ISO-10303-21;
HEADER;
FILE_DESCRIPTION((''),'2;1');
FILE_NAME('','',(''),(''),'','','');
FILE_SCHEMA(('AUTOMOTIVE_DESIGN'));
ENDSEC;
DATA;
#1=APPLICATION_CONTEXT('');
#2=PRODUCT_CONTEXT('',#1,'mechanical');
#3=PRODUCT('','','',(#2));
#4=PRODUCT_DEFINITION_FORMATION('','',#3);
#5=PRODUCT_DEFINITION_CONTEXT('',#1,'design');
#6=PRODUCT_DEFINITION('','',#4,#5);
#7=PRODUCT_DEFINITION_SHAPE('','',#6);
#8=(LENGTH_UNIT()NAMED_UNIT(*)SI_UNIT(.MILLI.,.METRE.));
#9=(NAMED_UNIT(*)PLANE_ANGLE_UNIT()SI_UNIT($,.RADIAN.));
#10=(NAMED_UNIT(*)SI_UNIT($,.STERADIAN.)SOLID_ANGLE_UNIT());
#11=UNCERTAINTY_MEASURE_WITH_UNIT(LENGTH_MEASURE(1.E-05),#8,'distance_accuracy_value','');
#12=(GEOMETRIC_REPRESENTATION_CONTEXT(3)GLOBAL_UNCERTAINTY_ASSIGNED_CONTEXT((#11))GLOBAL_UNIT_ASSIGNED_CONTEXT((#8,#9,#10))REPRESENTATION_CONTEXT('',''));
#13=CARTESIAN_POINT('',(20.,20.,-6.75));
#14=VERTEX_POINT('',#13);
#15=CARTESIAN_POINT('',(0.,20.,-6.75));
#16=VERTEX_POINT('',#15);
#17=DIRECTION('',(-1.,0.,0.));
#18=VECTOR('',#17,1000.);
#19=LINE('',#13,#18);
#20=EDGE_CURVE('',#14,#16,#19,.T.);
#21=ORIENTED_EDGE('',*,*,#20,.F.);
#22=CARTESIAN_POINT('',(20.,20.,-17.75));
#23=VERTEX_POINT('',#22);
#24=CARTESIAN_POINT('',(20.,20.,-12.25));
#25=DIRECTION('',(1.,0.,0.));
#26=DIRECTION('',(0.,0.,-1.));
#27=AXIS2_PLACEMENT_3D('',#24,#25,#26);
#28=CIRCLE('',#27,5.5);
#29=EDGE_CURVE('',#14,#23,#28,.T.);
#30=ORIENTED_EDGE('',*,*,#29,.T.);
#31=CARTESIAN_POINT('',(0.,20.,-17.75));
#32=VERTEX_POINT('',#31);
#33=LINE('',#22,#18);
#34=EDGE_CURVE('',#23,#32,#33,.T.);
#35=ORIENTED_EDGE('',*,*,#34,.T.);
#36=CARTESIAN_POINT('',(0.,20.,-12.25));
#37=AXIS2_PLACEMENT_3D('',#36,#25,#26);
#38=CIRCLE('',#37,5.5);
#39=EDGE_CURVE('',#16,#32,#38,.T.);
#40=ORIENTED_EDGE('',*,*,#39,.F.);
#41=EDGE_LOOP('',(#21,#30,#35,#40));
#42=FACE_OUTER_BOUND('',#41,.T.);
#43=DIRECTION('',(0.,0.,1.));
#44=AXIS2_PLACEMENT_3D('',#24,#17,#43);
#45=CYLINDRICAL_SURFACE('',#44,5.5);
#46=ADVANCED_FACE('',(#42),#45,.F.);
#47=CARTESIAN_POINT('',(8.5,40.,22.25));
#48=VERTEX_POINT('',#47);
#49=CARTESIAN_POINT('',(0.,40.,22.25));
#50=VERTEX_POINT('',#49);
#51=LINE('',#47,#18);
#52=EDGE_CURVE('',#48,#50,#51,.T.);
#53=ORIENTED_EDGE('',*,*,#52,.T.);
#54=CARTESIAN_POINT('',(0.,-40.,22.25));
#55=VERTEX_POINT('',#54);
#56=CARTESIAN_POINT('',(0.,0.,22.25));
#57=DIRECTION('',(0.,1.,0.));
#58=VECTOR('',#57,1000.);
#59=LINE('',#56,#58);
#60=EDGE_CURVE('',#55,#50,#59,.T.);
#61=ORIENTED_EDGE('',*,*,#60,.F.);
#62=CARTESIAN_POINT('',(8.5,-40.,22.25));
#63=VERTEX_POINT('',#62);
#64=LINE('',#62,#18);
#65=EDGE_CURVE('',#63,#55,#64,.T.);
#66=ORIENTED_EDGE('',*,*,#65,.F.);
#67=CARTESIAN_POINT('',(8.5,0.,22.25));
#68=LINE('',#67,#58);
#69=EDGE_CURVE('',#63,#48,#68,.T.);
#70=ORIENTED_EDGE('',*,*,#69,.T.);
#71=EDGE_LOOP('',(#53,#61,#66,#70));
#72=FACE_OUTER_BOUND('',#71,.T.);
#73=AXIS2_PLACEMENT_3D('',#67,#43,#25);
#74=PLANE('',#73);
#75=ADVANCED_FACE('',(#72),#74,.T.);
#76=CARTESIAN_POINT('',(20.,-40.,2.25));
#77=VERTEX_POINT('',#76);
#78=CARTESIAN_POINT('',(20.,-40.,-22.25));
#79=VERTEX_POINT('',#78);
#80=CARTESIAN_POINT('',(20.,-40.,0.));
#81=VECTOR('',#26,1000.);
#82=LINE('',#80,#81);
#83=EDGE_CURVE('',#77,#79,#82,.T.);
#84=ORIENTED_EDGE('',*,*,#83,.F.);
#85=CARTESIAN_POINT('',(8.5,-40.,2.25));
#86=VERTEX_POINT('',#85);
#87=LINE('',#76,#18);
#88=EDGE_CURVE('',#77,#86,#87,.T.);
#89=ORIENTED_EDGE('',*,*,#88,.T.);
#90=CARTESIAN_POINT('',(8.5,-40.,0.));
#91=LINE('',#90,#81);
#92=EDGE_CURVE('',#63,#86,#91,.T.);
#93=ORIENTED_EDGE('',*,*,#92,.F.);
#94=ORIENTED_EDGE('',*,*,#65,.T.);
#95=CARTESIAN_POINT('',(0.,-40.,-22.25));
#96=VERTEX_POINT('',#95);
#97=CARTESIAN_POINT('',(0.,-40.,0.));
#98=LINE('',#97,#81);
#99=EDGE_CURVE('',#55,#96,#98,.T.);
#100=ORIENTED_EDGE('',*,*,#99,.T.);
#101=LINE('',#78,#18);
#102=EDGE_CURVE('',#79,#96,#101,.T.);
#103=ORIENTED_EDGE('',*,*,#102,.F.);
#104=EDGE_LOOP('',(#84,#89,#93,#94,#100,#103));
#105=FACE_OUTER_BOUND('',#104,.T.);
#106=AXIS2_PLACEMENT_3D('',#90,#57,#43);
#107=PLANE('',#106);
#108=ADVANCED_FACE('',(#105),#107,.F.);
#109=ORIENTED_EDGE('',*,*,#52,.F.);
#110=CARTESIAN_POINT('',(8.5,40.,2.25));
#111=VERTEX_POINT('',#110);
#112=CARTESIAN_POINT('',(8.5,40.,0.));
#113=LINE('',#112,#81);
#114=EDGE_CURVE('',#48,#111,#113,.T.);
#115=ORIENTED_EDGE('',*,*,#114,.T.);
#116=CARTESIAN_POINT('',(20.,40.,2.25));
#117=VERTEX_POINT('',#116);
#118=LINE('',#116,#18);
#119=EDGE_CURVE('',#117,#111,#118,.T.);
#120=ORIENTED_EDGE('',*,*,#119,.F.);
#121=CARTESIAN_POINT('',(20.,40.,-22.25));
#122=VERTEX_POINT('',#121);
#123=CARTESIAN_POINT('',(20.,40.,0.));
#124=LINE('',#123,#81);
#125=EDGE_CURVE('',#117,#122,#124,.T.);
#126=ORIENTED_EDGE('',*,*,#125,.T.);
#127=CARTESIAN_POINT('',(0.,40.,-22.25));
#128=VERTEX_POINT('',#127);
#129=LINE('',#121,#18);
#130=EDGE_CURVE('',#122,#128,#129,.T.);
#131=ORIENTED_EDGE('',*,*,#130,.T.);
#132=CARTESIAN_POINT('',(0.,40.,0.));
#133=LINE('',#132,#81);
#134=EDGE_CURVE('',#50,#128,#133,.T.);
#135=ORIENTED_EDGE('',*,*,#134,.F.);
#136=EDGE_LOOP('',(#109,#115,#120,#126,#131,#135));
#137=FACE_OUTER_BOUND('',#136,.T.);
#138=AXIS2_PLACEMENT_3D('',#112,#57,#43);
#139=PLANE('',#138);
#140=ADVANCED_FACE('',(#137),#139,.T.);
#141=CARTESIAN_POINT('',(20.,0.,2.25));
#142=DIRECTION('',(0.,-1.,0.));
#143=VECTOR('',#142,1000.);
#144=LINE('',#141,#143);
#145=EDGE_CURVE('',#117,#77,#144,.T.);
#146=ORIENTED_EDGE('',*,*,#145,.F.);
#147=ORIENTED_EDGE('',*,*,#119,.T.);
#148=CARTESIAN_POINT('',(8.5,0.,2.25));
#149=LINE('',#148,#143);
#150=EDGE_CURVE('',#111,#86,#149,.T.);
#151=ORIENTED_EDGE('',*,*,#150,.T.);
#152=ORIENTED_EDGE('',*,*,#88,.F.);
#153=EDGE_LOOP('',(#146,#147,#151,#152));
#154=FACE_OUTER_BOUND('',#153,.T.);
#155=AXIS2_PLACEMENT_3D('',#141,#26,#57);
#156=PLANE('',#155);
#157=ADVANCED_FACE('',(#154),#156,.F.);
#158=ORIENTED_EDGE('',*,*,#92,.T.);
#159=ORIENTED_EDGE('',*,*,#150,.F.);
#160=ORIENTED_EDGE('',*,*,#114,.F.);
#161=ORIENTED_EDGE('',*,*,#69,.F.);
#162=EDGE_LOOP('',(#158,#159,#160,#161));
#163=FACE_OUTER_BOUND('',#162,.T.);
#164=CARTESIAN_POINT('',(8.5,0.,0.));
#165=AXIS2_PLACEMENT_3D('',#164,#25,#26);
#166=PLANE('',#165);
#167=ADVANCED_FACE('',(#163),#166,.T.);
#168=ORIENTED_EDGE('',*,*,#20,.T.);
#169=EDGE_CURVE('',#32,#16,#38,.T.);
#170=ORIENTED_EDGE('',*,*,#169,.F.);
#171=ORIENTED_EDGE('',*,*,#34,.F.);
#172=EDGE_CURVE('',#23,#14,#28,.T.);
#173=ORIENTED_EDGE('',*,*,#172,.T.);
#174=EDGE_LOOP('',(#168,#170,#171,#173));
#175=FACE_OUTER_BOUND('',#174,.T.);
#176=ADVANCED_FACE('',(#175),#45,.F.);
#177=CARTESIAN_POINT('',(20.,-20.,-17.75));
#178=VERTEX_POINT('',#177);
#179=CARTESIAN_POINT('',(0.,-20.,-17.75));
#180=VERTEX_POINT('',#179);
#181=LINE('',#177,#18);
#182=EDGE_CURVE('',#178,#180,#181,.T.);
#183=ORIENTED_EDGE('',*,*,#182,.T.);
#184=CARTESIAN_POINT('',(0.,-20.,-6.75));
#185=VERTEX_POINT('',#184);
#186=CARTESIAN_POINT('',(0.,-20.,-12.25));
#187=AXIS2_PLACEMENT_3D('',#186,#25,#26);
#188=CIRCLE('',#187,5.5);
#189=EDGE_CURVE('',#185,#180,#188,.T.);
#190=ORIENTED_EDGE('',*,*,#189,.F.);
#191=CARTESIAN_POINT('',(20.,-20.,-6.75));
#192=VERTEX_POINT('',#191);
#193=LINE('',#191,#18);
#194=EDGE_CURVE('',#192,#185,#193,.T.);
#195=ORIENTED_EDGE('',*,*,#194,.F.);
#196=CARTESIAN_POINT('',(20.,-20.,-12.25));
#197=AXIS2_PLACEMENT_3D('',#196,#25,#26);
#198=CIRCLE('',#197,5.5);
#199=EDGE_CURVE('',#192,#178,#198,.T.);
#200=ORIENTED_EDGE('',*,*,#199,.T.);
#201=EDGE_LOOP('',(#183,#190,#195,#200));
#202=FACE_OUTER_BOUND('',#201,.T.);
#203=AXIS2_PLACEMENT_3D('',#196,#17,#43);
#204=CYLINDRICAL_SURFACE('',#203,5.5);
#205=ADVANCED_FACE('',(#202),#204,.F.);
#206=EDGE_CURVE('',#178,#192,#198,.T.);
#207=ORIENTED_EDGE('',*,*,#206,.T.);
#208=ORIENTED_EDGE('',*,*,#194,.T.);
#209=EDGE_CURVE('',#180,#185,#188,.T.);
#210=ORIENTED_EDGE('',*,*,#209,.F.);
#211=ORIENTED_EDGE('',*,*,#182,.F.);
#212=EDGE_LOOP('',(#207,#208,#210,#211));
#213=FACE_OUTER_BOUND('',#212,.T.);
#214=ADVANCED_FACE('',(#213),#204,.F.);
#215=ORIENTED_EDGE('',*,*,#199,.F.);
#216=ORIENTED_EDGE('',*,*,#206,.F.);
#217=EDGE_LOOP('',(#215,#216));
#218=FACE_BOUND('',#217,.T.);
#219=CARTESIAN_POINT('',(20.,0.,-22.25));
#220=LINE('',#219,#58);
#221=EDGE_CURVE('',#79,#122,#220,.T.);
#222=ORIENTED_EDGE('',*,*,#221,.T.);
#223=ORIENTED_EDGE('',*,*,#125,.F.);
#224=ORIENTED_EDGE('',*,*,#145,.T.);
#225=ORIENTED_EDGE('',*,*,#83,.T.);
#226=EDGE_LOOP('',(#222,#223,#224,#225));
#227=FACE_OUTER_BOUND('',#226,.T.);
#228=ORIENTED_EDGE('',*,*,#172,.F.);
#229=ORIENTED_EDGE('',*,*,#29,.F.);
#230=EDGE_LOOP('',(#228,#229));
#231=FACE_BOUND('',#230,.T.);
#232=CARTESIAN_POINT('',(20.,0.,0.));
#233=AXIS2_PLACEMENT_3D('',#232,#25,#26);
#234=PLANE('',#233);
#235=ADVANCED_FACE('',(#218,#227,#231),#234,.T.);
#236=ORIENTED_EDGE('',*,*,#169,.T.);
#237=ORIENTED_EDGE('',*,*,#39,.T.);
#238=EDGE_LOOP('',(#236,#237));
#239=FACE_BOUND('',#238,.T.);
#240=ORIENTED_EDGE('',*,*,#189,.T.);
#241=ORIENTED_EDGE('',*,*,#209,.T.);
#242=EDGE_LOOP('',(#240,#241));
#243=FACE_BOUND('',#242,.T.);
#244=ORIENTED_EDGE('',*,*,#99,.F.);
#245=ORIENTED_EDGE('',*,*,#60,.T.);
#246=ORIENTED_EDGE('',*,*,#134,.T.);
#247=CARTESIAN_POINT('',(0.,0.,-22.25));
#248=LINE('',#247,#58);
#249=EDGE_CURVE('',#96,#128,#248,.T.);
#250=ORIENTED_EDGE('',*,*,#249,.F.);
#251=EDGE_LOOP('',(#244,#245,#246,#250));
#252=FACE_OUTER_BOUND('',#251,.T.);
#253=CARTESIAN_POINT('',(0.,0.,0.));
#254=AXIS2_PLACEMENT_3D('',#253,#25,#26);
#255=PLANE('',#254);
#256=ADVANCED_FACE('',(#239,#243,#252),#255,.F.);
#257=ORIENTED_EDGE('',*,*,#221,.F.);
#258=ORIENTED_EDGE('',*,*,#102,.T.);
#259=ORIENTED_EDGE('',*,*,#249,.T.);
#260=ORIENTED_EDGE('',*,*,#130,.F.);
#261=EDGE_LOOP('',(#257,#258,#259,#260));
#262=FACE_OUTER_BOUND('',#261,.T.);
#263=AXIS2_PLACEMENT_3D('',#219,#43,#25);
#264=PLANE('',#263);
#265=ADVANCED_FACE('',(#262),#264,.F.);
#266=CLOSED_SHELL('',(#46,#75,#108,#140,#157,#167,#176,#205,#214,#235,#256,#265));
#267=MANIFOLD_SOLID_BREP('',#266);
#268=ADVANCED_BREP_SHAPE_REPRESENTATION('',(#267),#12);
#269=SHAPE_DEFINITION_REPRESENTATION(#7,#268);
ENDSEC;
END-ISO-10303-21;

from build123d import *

# Parameters (mm, degrees)
SKETCH_1_3_W        = 20
SKETCH_1_3_H        = 80
BOSS_EXTRUDE1_DEPTH = 8.5
SKETCH_1_3_2_W      = 24.5
SKETCH_1_3_2_H      = 80
SKETCH_1_3_2_R      = 5.5
BOSS_EXTRUDE2_DEPTH = 20


with BuildPart() as part:
    # Sketch 1_3 → Boss-Extrude1 (new body)
    with BuildSketch(Plane(origin=(0, 0, 0), x_dir=(0, 0, -1), z_dir=(1, 0, 0))):
        with Locations((-12.25, 0)):
            Rectangle(SKETCH_1_3_W, SKETCH_1_3_H)
    extrude(amount=BOSS_EXTRUDE1_DEPTH)

    # Sketch 1_3 2 → Boss-Extrude2 (add)
    with BuildSketch(Plane(origin=(0, 0, 0), x_dir=(0, 0, -1), z_dir=(1, 0, 0))):
        with Locations((10, 0)):
            Rectangle(SKETCH_1_3_2_W, SKETCH_1_3_2_H)
        with Locations((12.25, -20)):
            Circle(SKETCH_1_3_2_R, mode=Mode.SUBTRACT)
        with Locations((12.25, 20)):
            Circle(SKETCH_1_3_2_R, mode=Mode.SUBTRACT)
    extrude(amount=BOSS_EXTRUDE2_DEPTH)


solid = part.part
